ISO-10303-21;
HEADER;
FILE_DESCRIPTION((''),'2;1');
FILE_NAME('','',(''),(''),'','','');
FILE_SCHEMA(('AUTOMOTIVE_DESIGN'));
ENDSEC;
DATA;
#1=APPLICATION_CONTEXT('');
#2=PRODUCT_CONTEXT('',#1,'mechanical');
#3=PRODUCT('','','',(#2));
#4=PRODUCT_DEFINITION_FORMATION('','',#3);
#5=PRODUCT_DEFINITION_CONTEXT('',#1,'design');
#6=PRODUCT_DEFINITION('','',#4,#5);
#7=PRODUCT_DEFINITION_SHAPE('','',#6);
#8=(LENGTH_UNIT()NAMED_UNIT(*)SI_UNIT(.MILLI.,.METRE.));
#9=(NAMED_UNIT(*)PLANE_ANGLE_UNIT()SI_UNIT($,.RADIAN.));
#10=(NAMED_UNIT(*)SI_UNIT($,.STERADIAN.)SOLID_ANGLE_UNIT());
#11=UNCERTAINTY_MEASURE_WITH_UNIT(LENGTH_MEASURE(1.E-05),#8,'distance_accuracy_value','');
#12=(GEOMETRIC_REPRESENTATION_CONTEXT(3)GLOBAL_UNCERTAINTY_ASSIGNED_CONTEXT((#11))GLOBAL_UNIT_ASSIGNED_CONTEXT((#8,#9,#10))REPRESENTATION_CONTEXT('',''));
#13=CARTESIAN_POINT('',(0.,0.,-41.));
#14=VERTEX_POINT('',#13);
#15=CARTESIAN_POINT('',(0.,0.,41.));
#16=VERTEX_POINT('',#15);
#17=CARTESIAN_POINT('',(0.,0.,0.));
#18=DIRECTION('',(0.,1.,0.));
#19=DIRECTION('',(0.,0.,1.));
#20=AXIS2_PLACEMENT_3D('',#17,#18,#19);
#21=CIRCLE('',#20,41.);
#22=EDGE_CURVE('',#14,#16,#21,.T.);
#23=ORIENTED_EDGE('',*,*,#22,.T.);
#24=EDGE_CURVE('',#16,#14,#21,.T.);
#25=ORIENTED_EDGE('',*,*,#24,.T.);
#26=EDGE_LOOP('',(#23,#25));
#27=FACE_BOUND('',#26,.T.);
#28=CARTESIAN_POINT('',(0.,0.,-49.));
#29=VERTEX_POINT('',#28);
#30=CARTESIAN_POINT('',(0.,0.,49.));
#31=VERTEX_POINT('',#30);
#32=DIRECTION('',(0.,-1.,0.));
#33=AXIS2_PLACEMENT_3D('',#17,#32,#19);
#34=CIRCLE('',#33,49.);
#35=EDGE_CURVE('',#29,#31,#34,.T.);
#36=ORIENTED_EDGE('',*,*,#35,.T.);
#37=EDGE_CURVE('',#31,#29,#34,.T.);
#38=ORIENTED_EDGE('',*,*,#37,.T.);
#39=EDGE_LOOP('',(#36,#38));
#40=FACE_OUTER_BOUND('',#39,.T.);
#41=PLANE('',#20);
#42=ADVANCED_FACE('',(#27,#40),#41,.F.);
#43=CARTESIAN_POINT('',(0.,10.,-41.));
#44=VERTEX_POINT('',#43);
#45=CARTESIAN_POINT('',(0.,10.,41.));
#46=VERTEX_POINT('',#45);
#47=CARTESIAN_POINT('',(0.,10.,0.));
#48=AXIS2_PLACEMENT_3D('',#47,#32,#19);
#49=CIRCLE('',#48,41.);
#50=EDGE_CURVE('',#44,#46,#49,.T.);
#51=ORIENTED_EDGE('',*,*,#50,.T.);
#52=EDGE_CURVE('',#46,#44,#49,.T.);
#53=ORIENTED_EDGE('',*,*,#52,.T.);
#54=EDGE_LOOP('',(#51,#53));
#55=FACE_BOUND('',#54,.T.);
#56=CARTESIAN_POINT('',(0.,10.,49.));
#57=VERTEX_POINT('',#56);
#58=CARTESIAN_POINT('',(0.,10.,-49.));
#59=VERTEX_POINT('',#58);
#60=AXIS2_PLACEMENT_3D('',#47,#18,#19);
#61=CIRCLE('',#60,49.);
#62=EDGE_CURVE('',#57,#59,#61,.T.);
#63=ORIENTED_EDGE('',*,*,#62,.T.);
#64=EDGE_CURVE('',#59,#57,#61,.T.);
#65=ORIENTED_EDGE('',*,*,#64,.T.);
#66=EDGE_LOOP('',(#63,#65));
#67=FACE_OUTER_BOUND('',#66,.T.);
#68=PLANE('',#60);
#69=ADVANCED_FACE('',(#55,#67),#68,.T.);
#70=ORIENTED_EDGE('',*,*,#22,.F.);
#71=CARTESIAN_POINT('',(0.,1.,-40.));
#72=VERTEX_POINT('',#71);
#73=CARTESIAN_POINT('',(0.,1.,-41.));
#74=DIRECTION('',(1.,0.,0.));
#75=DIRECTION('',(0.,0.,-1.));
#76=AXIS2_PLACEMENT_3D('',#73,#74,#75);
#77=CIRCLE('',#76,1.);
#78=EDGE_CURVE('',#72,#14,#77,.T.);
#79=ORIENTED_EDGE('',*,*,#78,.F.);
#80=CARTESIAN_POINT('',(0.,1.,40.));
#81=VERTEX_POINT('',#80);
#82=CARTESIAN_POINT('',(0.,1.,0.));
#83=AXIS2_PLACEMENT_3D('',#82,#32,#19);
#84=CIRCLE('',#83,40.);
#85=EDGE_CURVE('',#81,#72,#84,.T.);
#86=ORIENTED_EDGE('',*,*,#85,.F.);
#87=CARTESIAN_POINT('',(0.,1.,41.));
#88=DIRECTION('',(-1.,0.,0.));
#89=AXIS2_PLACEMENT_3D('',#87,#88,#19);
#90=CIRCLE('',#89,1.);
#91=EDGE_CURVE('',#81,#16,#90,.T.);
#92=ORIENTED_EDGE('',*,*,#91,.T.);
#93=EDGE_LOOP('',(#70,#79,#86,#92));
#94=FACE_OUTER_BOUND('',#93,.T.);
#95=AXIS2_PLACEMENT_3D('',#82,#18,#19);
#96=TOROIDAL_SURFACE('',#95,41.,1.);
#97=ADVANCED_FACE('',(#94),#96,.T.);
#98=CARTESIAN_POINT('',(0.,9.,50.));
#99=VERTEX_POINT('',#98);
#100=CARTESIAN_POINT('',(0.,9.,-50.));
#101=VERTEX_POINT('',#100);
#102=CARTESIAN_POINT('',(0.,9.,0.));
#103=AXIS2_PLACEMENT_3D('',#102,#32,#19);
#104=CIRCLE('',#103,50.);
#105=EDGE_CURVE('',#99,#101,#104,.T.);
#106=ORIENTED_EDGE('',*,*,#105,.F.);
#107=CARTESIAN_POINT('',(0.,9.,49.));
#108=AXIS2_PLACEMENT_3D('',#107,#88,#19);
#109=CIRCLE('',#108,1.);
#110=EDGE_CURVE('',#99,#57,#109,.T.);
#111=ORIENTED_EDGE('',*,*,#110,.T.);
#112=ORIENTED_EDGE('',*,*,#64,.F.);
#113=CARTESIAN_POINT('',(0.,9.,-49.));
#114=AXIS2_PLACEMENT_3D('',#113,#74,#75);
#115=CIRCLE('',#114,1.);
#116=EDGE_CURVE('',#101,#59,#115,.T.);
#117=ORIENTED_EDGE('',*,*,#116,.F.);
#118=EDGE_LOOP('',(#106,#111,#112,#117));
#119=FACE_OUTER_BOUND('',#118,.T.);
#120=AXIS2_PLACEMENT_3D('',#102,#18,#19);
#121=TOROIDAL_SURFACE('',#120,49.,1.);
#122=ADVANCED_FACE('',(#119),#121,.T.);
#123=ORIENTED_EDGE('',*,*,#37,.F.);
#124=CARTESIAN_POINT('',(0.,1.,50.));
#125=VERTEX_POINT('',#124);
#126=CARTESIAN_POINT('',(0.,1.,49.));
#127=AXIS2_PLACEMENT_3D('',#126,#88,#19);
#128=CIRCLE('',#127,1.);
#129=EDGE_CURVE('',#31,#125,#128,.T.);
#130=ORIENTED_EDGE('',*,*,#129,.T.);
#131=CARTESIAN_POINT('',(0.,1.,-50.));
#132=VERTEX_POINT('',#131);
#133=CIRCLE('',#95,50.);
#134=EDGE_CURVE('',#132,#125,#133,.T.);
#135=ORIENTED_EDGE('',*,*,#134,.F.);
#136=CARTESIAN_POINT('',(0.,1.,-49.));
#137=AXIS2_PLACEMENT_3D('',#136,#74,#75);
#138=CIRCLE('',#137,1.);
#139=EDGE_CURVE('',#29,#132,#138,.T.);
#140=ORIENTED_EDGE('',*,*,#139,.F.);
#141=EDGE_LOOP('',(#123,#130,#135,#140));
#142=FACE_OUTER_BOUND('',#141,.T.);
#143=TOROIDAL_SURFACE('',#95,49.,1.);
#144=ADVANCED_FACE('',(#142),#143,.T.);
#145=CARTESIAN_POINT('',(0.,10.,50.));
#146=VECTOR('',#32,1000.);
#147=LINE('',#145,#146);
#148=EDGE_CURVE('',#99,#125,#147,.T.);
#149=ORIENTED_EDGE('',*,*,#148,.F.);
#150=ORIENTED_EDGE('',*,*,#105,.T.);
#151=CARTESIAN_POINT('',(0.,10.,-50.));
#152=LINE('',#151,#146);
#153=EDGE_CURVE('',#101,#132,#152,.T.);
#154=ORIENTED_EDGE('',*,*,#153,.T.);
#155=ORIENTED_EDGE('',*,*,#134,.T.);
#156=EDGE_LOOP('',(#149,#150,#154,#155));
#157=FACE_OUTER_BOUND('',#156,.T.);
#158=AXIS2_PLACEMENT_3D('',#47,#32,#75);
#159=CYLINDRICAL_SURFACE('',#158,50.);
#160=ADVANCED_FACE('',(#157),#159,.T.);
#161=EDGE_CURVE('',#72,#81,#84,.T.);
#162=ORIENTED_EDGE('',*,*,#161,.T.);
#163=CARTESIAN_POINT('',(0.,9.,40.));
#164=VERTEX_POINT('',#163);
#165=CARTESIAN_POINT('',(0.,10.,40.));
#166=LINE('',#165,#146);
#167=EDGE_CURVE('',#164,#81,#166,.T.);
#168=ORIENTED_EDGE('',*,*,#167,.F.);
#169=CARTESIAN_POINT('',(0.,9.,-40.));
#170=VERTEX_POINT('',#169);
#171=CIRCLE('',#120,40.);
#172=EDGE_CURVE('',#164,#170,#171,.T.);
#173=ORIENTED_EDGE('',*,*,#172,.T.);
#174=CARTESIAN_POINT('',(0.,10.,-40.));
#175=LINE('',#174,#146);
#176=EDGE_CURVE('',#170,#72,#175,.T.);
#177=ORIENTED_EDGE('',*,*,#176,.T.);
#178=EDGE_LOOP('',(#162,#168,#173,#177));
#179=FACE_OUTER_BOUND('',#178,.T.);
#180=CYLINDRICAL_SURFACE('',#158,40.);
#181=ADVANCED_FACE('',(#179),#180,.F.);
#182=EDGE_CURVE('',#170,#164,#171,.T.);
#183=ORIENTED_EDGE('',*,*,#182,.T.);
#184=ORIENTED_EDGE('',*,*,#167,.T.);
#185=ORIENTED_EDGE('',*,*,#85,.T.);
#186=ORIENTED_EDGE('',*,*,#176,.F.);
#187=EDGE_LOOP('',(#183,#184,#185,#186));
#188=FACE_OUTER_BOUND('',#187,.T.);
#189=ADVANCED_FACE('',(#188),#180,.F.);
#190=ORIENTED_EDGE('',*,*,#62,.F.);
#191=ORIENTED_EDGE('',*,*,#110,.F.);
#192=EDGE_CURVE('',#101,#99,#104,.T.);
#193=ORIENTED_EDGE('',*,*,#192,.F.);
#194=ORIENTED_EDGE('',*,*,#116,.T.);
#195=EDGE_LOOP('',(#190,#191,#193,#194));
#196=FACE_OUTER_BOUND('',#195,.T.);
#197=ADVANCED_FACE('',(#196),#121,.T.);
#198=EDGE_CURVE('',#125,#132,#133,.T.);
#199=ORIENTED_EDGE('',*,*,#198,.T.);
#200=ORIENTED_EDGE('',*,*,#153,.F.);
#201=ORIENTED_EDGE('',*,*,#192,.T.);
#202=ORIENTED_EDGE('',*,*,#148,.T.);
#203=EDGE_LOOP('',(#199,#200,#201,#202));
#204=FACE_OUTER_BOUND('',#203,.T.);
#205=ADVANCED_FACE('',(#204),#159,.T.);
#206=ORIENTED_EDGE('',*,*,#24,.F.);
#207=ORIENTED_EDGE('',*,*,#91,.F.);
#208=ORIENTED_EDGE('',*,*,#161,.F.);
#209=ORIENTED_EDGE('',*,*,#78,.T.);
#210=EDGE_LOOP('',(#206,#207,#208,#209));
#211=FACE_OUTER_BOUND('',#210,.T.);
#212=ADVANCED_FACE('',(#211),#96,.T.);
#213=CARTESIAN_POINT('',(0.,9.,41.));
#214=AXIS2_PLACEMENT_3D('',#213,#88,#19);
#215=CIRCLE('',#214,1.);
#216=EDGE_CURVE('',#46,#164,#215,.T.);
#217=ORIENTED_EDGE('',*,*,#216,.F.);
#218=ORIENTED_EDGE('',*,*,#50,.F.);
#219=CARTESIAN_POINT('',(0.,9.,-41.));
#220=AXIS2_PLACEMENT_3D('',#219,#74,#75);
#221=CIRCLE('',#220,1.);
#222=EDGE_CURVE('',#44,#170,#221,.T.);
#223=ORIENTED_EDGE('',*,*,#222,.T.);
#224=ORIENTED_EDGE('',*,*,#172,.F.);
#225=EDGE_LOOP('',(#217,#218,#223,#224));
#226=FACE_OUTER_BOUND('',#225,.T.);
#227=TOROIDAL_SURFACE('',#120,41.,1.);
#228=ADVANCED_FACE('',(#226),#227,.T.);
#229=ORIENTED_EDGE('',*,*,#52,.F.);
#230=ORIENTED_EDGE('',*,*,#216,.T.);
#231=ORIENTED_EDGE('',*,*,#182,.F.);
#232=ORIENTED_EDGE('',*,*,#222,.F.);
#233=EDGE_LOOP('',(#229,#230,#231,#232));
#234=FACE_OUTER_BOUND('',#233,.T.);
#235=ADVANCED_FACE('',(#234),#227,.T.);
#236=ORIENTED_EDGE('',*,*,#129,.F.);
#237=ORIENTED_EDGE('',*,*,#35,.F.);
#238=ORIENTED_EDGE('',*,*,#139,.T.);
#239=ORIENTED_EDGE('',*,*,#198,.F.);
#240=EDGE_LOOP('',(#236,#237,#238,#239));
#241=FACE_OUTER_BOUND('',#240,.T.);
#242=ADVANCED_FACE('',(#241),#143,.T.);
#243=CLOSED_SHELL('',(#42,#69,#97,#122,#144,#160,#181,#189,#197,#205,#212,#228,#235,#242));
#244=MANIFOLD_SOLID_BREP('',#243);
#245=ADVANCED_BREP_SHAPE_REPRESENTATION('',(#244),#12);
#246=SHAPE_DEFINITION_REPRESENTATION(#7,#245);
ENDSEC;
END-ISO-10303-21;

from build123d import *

# Parameters (mm, degrees)
SKETCH_1_R      = 50
SKETCH_1_R_2    = 40
EXTRUDE_1_DEPTH = 10
FILLET_1_R      = 1


with BuildPart() as part:
    # 草图1 → 凸台-拉伸1 (new body)
    with BuildSketch(Plane(origin=(0, 0, 0), x_dir=(1, 0, 0), z_dir=(0, 1, 0))):
        with Locations(Location((0, 0, 0), (0, 0, 270))):
            Circle(SKETCH_1_R)
        with Locations(Location((0, 0, 0), (0, 0, 270))):
            Circle(SKETCH_1_R_2, mode=Mode.SUBTRACT)
    extrude(amount=EXTRUDE_1_DEPTH)

    # 圆角1
    fillet_1_edges = [part.edges().sort_by_distance(p)[0] for p in [
        (0, 0, -50),
        (0, 10, -50),
        (0, 0, -40),
        (0, 10, -40),
    ]]
    fillet(fillet_1_edges, radius=FILLET_1_R)


solid = part.part
